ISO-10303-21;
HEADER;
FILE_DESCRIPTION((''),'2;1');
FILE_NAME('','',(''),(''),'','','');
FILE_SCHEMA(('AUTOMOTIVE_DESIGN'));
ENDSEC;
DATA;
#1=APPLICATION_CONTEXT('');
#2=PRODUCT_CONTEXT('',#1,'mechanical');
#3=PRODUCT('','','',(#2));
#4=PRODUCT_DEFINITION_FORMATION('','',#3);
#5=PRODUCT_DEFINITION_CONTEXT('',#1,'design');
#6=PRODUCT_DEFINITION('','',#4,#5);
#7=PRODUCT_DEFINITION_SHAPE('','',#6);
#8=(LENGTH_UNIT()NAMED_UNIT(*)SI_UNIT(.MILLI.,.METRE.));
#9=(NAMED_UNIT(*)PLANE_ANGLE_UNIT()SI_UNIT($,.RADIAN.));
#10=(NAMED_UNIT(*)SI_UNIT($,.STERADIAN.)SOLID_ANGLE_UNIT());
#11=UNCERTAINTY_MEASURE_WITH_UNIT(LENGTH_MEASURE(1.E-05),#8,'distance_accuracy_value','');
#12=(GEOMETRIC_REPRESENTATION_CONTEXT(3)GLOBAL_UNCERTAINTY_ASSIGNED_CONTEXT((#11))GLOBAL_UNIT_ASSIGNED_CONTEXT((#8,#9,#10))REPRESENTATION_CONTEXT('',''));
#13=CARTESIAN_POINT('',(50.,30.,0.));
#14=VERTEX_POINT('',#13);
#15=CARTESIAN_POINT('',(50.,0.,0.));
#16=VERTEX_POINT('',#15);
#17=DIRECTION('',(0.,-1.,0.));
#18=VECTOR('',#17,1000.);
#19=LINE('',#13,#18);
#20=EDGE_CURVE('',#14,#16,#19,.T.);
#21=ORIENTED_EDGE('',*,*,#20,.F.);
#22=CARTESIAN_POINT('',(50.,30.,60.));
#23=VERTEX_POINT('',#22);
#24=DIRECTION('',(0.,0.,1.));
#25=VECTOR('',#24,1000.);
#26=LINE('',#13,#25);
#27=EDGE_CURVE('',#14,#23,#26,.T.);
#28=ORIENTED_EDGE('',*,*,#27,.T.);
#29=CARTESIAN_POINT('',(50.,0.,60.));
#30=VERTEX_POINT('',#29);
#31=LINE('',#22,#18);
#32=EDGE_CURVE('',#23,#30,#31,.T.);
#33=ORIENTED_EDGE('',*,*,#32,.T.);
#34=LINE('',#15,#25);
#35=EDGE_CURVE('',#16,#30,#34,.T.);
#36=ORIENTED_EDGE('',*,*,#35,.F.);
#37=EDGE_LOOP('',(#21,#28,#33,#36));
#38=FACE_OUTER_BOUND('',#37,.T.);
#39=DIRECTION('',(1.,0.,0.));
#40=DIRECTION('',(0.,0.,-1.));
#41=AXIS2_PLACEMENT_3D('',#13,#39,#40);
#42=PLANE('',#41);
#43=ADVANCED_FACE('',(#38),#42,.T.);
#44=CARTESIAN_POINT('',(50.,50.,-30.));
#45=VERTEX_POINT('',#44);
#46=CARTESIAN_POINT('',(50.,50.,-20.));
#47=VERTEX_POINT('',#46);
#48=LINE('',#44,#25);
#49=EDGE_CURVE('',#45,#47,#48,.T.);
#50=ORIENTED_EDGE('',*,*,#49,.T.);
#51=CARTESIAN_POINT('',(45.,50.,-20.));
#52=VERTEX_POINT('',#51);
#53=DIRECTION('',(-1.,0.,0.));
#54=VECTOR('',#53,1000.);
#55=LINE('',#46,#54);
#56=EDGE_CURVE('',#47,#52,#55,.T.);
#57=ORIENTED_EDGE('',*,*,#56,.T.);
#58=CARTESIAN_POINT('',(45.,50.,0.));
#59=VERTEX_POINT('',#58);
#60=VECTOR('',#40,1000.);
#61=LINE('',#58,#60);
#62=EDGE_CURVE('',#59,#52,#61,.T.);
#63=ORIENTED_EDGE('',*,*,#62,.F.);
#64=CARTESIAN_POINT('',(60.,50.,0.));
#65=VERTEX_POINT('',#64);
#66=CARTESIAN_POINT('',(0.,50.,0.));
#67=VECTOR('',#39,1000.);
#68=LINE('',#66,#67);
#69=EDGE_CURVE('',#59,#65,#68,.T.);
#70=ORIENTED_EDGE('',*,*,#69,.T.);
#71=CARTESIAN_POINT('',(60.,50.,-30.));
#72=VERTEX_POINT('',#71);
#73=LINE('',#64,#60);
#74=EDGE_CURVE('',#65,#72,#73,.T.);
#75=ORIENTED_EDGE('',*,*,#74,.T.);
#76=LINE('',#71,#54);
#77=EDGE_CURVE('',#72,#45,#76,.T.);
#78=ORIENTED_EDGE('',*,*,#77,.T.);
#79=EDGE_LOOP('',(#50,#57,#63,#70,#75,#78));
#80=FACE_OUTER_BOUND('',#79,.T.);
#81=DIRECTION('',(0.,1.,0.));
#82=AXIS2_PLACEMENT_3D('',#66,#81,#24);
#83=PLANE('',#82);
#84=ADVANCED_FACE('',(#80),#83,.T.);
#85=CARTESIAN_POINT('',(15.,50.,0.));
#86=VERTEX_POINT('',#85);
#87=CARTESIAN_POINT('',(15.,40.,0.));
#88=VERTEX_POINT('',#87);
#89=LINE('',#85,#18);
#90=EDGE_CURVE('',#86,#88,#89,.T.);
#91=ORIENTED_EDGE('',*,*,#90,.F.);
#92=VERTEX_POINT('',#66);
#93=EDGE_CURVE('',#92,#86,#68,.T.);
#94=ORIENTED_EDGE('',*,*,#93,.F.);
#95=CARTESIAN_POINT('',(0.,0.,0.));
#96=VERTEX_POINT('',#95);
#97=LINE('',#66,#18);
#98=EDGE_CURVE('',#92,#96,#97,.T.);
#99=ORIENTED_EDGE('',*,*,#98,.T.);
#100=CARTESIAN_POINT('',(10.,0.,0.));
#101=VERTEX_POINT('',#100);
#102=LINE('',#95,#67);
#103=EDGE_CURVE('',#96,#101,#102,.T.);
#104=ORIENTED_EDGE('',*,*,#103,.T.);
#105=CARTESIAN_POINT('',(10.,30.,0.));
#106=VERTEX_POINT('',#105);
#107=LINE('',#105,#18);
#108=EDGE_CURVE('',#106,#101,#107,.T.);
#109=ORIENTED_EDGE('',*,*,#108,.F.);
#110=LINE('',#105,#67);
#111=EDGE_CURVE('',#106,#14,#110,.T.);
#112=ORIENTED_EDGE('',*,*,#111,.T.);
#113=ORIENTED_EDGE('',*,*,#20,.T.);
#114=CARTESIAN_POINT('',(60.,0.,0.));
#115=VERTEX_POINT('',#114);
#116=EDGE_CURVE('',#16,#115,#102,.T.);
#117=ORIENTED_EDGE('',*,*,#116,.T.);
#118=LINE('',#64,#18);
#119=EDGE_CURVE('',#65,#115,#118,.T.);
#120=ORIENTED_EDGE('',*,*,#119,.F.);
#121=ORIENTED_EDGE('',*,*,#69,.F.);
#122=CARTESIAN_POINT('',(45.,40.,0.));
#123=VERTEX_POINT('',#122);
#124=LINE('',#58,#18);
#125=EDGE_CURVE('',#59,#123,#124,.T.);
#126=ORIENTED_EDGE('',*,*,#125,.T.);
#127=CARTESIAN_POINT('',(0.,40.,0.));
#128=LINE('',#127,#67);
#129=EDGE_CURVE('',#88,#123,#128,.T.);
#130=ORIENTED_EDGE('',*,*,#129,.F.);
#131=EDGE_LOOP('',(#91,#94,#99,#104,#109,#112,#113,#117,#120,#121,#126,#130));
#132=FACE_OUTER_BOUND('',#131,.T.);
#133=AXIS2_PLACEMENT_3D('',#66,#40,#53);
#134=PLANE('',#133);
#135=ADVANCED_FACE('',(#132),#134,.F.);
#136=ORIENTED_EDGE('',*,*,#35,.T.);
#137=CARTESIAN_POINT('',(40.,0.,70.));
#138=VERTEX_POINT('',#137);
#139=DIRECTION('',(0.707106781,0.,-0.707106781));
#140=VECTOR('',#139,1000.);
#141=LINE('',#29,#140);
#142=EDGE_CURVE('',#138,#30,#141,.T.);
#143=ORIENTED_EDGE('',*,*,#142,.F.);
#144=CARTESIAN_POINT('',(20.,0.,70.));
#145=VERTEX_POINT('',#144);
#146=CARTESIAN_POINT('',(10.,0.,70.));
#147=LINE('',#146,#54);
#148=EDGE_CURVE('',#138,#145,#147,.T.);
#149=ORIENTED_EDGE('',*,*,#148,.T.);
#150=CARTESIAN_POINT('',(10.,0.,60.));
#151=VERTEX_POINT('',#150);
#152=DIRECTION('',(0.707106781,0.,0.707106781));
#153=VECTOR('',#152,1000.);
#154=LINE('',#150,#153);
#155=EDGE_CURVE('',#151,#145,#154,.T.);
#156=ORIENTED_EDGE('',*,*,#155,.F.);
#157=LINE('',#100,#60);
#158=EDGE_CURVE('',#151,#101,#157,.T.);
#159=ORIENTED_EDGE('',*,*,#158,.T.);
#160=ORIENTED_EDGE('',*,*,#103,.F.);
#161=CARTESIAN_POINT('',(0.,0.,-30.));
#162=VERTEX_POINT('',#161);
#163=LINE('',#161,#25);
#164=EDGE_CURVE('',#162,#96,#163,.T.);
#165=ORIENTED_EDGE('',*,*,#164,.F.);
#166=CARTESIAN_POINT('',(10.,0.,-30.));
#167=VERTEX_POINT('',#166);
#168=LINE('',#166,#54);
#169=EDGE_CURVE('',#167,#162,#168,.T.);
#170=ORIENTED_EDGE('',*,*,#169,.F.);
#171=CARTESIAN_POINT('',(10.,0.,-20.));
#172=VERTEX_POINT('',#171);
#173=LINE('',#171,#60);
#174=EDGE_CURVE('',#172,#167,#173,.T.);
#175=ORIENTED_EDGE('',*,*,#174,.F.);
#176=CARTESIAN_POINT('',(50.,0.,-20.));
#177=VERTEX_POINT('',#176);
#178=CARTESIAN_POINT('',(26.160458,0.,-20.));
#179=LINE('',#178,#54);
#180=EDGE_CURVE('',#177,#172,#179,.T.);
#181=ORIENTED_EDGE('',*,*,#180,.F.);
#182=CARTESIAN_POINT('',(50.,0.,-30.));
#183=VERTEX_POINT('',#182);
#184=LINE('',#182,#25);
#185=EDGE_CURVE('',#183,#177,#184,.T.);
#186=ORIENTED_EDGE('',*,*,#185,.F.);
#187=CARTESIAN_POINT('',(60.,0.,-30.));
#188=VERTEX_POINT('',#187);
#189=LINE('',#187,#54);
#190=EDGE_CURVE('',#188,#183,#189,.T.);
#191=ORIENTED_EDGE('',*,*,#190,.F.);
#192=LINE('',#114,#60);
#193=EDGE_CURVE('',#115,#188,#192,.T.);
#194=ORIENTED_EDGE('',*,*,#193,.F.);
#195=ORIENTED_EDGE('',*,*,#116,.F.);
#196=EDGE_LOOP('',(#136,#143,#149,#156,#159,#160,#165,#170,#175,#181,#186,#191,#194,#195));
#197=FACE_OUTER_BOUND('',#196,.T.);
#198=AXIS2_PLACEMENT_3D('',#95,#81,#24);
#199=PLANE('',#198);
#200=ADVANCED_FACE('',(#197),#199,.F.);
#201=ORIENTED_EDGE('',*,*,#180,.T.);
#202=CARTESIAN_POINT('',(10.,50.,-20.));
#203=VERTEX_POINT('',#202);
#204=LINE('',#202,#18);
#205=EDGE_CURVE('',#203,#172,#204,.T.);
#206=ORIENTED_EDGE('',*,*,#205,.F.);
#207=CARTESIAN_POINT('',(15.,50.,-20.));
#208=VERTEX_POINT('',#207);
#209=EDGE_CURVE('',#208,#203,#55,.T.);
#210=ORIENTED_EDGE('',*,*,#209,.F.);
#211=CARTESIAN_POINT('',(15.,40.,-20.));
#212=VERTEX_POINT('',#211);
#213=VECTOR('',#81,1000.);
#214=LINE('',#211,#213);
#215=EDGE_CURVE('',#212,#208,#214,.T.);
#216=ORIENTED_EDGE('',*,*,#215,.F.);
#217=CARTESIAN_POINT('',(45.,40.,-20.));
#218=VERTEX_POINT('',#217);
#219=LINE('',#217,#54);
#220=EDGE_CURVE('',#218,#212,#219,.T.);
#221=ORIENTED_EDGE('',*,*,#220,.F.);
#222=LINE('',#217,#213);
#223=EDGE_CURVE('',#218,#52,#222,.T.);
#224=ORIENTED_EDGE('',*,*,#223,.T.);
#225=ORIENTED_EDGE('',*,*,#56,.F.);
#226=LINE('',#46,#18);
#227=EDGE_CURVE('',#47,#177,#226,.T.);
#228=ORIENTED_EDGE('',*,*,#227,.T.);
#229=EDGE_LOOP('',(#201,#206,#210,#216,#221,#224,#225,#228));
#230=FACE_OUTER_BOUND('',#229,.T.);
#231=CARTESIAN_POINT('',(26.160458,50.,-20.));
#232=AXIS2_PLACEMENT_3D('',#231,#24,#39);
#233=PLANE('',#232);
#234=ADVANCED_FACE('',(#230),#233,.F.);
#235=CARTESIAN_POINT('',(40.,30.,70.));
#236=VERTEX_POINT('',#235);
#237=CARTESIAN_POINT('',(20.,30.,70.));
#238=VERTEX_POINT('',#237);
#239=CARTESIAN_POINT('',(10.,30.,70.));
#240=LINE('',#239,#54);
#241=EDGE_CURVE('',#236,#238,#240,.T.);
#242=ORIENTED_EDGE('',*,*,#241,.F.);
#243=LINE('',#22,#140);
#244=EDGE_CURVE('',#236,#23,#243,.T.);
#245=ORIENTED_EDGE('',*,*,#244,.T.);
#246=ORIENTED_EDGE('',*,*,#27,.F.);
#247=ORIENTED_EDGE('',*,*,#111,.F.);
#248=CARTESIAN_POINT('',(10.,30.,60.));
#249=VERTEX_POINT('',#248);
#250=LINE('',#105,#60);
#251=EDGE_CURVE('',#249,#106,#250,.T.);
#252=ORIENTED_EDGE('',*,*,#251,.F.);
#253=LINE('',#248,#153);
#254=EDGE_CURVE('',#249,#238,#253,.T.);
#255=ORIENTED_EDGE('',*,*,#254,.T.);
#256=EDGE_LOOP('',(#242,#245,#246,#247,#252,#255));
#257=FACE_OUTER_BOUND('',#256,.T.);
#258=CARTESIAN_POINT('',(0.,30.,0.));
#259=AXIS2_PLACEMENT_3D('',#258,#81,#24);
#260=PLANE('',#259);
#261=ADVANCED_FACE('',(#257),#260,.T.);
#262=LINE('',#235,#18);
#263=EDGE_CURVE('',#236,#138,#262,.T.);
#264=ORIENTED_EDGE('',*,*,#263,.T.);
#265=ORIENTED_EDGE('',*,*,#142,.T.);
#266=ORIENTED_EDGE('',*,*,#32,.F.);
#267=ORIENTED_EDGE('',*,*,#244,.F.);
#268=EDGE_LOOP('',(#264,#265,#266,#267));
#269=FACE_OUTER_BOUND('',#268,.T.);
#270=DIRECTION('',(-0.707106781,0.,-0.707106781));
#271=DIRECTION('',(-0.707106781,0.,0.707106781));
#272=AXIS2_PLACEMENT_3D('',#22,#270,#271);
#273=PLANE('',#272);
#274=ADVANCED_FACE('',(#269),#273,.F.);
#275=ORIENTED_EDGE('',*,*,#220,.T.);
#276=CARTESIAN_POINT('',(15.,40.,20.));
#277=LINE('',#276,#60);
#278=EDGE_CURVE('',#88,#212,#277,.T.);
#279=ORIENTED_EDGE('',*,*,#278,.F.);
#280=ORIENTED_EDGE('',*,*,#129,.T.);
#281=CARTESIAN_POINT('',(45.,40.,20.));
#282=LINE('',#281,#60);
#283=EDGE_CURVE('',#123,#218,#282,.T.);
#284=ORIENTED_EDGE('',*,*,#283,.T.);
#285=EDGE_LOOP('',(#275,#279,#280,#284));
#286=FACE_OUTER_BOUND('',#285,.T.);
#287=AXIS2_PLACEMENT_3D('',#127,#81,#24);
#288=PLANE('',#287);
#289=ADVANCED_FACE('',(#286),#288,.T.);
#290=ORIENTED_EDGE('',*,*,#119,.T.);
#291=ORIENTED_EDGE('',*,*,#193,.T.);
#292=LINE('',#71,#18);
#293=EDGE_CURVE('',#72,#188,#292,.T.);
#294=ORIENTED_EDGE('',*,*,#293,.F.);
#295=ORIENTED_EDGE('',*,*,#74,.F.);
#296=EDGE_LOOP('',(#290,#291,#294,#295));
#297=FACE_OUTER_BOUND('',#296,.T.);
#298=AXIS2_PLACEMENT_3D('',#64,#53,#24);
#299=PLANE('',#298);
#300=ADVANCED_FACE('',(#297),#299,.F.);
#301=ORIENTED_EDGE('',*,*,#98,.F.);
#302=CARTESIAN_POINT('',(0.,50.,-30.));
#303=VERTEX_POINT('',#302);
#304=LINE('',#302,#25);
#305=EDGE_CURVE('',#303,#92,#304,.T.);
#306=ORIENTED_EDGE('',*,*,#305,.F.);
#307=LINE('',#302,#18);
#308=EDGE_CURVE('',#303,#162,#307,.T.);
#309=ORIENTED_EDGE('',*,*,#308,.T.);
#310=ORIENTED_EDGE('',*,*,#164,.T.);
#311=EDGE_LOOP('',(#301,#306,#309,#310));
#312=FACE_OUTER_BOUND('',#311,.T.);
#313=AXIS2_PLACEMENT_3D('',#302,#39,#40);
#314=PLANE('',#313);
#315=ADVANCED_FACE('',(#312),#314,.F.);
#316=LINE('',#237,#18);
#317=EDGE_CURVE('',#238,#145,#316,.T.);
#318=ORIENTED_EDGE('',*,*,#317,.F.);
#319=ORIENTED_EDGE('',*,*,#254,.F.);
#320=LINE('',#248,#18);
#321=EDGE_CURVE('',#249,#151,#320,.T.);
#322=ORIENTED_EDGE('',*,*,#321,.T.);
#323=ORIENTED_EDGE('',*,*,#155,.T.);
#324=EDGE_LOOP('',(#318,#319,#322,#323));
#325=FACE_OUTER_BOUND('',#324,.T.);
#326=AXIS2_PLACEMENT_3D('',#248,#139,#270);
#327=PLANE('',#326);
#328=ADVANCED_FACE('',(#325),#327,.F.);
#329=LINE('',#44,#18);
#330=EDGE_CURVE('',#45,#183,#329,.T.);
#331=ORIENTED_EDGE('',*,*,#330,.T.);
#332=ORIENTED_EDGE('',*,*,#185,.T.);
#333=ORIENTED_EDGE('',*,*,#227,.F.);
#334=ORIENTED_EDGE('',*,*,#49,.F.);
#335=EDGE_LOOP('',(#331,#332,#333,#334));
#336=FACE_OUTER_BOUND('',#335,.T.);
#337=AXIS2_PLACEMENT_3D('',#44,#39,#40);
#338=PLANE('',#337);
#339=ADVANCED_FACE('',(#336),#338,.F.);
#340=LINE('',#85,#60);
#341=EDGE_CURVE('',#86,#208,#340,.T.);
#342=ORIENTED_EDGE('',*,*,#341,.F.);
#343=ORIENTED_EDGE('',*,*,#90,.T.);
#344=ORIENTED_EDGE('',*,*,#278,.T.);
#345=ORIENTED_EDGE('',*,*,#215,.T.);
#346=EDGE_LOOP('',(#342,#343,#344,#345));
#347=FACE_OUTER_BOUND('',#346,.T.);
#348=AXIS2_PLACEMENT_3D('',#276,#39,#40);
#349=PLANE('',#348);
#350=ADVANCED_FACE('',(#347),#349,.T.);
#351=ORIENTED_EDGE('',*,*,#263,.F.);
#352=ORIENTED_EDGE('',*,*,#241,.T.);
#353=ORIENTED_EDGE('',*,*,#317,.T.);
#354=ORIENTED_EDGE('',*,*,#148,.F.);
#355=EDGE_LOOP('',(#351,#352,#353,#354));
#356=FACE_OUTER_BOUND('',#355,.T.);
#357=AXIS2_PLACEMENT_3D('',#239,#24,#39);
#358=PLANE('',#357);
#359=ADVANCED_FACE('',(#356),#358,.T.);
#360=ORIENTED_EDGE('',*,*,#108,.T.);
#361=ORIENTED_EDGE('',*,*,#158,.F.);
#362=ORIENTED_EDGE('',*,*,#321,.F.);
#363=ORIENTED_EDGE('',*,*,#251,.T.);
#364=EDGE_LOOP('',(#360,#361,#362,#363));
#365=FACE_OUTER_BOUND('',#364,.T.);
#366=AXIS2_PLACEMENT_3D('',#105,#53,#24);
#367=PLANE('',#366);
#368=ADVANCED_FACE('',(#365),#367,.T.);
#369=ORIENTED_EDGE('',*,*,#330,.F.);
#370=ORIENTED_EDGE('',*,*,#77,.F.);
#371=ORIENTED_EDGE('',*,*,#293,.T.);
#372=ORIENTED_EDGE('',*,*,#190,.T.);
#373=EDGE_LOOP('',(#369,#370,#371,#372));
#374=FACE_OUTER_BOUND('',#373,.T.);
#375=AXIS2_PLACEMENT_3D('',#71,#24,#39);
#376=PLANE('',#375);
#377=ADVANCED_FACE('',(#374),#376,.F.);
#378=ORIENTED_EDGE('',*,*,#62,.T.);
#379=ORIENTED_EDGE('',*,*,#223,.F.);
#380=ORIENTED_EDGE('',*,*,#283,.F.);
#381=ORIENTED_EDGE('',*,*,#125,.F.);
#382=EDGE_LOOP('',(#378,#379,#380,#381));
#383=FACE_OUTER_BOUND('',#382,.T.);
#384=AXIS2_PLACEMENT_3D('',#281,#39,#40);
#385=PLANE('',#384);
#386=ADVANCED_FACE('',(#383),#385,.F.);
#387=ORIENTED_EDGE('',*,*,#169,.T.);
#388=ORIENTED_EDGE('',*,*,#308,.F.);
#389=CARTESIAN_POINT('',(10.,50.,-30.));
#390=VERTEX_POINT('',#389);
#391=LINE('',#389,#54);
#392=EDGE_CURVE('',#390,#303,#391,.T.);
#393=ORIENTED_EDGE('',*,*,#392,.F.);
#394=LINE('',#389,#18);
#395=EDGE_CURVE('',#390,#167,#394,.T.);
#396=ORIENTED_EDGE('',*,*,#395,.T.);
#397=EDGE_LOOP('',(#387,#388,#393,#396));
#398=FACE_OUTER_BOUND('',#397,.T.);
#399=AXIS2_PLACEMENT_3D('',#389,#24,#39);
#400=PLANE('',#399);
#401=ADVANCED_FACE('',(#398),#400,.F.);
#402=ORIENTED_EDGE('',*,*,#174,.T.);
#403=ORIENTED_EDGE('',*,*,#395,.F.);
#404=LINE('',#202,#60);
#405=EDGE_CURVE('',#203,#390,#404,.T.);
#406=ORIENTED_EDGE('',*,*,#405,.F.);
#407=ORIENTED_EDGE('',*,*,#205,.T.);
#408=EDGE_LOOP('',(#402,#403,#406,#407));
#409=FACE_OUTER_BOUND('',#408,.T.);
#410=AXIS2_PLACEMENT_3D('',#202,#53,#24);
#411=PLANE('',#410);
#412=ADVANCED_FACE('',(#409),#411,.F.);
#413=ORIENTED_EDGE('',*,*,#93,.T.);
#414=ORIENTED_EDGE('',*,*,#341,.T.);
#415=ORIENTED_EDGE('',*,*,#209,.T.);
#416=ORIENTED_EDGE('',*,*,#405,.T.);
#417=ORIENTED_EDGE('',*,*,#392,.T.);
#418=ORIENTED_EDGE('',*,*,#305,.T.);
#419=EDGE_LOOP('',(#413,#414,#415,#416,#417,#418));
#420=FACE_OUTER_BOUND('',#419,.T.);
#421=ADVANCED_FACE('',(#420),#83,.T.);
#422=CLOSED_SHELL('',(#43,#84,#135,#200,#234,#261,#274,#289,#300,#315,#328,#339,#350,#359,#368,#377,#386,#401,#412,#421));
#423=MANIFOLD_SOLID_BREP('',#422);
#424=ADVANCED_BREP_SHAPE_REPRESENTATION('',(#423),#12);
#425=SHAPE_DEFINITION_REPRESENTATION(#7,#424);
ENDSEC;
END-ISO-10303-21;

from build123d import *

# Parameters (mm, degrees)
CHAMFERED_BASE_BLOCK_DEPTH = 50
STEP_CUT_SKETCH_W          = 30
STEP_CUT_SKETCH_H          = 40
STEP_CUT_30X40_DEPTH       = 10
UPRIGHT_PROFILE_SKETCH_W   = 40
UPRIGHT_PROFILE_SKETCH_H   = 70
UPRIGHT_BLOCK_DEPTH        = 30
TOP_SLOT_CUT_DEPTH         = 30


with BuildPart() as part:
    # Base Profile Sketch → Chamfered Base Block (new body)
    with BuildSketch(Plane(origin=(0, 0, 0), x_dir=(1, 0, 0), z_dir=(0, 1, 0))):
        Polygon((0, 30), (0, 0), (60, 0), (60, 30), (50, 30), (50, 20), (26.160458453, 20), (10, 20), (10, 30), align=None)
    extrude(amount=CHAMFERED_BASE_BLOCK_DEPTH)

    # Step Cut Sketch → Step Cut 30x40 (cut)
    with BuildSketch(Plane(origin=(0, 50, 0), x_dir=(1, 0, 0), z_dir=(0, 1, 0))):
        with Locations((30, 0)):
            Rectangle(STEP_CUT_SKETCH_W, STEP_CUT_SKETCH_H)
    extrude(amount=-STEP_CUT_30X40_DEPTH, mode=Mode.SUBTRACT)

    # Upright Profile Sketch → Upright Block (add)
    with BuildSketch(Plane.XZ):
        with Locations((30, 35)):
            Rectangle(UPRIGHT_PROFILE_SKETCH_W, UPRIGHT_PROFILE_SKETCH_H)
    extrude(amount=-UPRIGHT_BLOCK_DEPTH)

    # Slot Sketch → Top Slot Cut (cut)
    with BuildSketch(Plane.XZ):
        Polygon((50, 60), (40, 70), (50, 70), align=None)
        Polygon((10, 70), (10, 60), (20, 70), align=None)
    extrude(amount=-TOP_SLOT_CUT_DEPTH, mode=Mode.SUBTRACT)


solid = part.part
